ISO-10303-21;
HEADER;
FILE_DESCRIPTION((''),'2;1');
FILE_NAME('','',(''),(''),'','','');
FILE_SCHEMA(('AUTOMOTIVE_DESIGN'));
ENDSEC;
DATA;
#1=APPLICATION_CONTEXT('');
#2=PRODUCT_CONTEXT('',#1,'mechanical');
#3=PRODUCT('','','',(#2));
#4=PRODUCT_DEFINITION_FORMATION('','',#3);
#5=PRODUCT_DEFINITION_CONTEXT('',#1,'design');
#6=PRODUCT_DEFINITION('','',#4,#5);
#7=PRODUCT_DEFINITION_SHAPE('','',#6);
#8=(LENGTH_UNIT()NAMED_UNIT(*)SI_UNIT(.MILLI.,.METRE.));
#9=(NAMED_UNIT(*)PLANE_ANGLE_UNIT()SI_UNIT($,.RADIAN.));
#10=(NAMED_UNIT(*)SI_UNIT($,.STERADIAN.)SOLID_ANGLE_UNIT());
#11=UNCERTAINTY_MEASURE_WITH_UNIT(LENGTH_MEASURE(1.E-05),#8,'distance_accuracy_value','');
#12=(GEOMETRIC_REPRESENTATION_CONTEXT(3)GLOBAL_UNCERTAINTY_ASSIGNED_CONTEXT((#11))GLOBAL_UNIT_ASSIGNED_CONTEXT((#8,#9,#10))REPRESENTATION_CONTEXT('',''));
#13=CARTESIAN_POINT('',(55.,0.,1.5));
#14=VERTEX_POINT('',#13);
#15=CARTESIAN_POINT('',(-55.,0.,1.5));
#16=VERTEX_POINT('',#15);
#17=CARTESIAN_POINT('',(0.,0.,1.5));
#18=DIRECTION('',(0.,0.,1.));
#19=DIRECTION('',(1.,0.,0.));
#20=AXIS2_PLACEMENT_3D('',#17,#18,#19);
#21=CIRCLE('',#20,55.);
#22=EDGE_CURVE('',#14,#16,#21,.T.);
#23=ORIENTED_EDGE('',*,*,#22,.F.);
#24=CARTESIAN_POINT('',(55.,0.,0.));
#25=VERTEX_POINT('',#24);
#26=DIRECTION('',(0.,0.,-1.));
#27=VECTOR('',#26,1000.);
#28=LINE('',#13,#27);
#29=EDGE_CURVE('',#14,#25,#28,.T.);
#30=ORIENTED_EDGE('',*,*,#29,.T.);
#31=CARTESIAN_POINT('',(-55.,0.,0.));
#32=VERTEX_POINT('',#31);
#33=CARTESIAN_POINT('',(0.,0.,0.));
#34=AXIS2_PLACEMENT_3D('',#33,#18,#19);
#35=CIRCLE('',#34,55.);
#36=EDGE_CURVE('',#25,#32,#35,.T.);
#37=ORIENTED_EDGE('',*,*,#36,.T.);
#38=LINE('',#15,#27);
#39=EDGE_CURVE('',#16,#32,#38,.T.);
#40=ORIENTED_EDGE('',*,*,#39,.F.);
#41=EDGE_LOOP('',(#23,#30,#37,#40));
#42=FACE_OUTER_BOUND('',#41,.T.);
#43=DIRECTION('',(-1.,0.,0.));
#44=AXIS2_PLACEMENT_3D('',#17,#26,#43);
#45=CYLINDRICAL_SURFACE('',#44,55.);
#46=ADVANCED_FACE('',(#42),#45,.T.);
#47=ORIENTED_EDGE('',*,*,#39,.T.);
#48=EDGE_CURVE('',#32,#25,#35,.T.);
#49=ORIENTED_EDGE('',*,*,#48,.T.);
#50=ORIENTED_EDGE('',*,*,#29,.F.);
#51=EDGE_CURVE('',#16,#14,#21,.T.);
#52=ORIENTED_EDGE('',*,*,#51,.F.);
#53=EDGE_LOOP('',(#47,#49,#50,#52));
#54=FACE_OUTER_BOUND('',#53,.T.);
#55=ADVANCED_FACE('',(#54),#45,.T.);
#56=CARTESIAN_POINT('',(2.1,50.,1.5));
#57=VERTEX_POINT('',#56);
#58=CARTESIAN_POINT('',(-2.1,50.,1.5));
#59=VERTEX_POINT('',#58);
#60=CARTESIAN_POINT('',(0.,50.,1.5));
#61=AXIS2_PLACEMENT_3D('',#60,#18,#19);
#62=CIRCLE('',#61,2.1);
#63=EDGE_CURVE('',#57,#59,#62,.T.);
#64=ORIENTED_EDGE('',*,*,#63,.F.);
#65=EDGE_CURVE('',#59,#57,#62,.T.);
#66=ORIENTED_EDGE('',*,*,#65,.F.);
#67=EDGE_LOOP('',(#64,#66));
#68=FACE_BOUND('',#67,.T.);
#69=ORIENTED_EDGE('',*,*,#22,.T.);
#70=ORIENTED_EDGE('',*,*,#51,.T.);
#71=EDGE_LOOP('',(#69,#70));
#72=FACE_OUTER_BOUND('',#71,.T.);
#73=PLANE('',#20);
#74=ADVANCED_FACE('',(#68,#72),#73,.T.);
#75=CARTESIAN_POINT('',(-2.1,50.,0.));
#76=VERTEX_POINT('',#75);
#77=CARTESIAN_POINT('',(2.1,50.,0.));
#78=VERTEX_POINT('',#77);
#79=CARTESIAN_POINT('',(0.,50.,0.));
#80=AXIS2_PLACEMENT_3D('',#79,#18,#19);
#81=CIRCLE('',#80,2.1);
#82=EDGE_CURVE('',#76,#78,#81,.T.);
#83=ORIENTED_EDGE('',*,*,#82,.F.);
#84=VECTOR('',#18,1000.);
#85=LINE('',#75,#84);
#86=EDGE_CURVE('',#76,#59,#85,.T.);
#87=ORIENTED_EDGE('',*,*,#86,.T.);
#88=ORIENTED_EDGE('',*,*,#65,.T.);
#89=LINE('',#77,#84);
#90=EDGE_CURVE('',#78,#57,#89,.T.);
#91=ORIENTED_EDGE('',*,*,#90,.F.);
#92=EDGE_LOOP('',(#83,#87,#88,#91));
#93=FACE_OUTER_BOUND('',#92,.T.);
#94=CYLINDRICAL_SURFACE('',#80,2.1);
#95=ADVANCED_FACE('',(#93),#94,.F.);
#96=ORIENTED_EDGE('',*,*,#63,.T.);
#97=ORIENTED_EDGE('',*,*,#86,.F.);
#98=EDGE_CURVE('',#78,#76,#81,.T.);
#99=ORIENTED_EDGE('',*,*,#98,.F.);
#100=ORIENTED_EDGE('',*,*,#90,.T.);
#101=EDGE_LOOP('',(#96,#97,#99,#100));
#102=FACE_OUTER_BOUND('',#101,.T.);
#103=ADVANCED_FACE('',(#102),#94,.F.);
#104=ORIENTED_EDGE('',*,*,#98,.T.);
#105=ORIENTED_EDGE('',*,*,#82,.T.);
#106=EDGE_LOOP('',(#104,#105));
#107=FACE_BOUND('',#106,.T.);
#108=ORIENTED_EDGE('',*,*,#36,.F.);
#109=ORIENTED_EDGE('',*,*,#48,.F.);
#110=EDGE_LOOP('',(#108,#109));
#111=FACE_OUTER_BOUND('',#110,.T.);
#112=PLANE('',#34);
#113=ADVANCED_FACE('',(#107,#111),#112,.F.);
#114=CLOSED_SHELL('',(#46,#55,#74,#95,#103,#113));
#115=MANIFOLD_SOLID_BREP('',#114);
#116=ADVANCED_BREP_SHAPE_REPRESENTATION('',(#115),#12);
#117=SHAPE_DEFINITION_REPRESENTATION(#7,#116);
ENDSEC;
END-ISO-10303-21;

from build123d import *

# Parameters (mm, degrees)
SKETCH_1_R          = 55
EXTRUDE_1_DEPTH     = 1.5
SKETCH_2_R          = 2.1
CUT_EXTRUDE_1_DEPTH = 1.5


with BuildPart() as part:
    # 草图1 → 凸台-拉伸1 (new body)
    with BuildSketch(Plane.XY):
        Circle(SKETCH_1_R)
    extrude(amount=EXTRUDE_1_DEPTH)

    # 草图2 → 切除-拉伸1 (cut)
    with BuildSketch(Plane.XY.offset(1.5)):
        with Locations((0, 50)):
            Circle(SKETCH_2_R)
    extrude(amount=-CUT_EXTRUDE_1_DEPTH, mode=Mode.SUBTRACT)


solid = part.part
